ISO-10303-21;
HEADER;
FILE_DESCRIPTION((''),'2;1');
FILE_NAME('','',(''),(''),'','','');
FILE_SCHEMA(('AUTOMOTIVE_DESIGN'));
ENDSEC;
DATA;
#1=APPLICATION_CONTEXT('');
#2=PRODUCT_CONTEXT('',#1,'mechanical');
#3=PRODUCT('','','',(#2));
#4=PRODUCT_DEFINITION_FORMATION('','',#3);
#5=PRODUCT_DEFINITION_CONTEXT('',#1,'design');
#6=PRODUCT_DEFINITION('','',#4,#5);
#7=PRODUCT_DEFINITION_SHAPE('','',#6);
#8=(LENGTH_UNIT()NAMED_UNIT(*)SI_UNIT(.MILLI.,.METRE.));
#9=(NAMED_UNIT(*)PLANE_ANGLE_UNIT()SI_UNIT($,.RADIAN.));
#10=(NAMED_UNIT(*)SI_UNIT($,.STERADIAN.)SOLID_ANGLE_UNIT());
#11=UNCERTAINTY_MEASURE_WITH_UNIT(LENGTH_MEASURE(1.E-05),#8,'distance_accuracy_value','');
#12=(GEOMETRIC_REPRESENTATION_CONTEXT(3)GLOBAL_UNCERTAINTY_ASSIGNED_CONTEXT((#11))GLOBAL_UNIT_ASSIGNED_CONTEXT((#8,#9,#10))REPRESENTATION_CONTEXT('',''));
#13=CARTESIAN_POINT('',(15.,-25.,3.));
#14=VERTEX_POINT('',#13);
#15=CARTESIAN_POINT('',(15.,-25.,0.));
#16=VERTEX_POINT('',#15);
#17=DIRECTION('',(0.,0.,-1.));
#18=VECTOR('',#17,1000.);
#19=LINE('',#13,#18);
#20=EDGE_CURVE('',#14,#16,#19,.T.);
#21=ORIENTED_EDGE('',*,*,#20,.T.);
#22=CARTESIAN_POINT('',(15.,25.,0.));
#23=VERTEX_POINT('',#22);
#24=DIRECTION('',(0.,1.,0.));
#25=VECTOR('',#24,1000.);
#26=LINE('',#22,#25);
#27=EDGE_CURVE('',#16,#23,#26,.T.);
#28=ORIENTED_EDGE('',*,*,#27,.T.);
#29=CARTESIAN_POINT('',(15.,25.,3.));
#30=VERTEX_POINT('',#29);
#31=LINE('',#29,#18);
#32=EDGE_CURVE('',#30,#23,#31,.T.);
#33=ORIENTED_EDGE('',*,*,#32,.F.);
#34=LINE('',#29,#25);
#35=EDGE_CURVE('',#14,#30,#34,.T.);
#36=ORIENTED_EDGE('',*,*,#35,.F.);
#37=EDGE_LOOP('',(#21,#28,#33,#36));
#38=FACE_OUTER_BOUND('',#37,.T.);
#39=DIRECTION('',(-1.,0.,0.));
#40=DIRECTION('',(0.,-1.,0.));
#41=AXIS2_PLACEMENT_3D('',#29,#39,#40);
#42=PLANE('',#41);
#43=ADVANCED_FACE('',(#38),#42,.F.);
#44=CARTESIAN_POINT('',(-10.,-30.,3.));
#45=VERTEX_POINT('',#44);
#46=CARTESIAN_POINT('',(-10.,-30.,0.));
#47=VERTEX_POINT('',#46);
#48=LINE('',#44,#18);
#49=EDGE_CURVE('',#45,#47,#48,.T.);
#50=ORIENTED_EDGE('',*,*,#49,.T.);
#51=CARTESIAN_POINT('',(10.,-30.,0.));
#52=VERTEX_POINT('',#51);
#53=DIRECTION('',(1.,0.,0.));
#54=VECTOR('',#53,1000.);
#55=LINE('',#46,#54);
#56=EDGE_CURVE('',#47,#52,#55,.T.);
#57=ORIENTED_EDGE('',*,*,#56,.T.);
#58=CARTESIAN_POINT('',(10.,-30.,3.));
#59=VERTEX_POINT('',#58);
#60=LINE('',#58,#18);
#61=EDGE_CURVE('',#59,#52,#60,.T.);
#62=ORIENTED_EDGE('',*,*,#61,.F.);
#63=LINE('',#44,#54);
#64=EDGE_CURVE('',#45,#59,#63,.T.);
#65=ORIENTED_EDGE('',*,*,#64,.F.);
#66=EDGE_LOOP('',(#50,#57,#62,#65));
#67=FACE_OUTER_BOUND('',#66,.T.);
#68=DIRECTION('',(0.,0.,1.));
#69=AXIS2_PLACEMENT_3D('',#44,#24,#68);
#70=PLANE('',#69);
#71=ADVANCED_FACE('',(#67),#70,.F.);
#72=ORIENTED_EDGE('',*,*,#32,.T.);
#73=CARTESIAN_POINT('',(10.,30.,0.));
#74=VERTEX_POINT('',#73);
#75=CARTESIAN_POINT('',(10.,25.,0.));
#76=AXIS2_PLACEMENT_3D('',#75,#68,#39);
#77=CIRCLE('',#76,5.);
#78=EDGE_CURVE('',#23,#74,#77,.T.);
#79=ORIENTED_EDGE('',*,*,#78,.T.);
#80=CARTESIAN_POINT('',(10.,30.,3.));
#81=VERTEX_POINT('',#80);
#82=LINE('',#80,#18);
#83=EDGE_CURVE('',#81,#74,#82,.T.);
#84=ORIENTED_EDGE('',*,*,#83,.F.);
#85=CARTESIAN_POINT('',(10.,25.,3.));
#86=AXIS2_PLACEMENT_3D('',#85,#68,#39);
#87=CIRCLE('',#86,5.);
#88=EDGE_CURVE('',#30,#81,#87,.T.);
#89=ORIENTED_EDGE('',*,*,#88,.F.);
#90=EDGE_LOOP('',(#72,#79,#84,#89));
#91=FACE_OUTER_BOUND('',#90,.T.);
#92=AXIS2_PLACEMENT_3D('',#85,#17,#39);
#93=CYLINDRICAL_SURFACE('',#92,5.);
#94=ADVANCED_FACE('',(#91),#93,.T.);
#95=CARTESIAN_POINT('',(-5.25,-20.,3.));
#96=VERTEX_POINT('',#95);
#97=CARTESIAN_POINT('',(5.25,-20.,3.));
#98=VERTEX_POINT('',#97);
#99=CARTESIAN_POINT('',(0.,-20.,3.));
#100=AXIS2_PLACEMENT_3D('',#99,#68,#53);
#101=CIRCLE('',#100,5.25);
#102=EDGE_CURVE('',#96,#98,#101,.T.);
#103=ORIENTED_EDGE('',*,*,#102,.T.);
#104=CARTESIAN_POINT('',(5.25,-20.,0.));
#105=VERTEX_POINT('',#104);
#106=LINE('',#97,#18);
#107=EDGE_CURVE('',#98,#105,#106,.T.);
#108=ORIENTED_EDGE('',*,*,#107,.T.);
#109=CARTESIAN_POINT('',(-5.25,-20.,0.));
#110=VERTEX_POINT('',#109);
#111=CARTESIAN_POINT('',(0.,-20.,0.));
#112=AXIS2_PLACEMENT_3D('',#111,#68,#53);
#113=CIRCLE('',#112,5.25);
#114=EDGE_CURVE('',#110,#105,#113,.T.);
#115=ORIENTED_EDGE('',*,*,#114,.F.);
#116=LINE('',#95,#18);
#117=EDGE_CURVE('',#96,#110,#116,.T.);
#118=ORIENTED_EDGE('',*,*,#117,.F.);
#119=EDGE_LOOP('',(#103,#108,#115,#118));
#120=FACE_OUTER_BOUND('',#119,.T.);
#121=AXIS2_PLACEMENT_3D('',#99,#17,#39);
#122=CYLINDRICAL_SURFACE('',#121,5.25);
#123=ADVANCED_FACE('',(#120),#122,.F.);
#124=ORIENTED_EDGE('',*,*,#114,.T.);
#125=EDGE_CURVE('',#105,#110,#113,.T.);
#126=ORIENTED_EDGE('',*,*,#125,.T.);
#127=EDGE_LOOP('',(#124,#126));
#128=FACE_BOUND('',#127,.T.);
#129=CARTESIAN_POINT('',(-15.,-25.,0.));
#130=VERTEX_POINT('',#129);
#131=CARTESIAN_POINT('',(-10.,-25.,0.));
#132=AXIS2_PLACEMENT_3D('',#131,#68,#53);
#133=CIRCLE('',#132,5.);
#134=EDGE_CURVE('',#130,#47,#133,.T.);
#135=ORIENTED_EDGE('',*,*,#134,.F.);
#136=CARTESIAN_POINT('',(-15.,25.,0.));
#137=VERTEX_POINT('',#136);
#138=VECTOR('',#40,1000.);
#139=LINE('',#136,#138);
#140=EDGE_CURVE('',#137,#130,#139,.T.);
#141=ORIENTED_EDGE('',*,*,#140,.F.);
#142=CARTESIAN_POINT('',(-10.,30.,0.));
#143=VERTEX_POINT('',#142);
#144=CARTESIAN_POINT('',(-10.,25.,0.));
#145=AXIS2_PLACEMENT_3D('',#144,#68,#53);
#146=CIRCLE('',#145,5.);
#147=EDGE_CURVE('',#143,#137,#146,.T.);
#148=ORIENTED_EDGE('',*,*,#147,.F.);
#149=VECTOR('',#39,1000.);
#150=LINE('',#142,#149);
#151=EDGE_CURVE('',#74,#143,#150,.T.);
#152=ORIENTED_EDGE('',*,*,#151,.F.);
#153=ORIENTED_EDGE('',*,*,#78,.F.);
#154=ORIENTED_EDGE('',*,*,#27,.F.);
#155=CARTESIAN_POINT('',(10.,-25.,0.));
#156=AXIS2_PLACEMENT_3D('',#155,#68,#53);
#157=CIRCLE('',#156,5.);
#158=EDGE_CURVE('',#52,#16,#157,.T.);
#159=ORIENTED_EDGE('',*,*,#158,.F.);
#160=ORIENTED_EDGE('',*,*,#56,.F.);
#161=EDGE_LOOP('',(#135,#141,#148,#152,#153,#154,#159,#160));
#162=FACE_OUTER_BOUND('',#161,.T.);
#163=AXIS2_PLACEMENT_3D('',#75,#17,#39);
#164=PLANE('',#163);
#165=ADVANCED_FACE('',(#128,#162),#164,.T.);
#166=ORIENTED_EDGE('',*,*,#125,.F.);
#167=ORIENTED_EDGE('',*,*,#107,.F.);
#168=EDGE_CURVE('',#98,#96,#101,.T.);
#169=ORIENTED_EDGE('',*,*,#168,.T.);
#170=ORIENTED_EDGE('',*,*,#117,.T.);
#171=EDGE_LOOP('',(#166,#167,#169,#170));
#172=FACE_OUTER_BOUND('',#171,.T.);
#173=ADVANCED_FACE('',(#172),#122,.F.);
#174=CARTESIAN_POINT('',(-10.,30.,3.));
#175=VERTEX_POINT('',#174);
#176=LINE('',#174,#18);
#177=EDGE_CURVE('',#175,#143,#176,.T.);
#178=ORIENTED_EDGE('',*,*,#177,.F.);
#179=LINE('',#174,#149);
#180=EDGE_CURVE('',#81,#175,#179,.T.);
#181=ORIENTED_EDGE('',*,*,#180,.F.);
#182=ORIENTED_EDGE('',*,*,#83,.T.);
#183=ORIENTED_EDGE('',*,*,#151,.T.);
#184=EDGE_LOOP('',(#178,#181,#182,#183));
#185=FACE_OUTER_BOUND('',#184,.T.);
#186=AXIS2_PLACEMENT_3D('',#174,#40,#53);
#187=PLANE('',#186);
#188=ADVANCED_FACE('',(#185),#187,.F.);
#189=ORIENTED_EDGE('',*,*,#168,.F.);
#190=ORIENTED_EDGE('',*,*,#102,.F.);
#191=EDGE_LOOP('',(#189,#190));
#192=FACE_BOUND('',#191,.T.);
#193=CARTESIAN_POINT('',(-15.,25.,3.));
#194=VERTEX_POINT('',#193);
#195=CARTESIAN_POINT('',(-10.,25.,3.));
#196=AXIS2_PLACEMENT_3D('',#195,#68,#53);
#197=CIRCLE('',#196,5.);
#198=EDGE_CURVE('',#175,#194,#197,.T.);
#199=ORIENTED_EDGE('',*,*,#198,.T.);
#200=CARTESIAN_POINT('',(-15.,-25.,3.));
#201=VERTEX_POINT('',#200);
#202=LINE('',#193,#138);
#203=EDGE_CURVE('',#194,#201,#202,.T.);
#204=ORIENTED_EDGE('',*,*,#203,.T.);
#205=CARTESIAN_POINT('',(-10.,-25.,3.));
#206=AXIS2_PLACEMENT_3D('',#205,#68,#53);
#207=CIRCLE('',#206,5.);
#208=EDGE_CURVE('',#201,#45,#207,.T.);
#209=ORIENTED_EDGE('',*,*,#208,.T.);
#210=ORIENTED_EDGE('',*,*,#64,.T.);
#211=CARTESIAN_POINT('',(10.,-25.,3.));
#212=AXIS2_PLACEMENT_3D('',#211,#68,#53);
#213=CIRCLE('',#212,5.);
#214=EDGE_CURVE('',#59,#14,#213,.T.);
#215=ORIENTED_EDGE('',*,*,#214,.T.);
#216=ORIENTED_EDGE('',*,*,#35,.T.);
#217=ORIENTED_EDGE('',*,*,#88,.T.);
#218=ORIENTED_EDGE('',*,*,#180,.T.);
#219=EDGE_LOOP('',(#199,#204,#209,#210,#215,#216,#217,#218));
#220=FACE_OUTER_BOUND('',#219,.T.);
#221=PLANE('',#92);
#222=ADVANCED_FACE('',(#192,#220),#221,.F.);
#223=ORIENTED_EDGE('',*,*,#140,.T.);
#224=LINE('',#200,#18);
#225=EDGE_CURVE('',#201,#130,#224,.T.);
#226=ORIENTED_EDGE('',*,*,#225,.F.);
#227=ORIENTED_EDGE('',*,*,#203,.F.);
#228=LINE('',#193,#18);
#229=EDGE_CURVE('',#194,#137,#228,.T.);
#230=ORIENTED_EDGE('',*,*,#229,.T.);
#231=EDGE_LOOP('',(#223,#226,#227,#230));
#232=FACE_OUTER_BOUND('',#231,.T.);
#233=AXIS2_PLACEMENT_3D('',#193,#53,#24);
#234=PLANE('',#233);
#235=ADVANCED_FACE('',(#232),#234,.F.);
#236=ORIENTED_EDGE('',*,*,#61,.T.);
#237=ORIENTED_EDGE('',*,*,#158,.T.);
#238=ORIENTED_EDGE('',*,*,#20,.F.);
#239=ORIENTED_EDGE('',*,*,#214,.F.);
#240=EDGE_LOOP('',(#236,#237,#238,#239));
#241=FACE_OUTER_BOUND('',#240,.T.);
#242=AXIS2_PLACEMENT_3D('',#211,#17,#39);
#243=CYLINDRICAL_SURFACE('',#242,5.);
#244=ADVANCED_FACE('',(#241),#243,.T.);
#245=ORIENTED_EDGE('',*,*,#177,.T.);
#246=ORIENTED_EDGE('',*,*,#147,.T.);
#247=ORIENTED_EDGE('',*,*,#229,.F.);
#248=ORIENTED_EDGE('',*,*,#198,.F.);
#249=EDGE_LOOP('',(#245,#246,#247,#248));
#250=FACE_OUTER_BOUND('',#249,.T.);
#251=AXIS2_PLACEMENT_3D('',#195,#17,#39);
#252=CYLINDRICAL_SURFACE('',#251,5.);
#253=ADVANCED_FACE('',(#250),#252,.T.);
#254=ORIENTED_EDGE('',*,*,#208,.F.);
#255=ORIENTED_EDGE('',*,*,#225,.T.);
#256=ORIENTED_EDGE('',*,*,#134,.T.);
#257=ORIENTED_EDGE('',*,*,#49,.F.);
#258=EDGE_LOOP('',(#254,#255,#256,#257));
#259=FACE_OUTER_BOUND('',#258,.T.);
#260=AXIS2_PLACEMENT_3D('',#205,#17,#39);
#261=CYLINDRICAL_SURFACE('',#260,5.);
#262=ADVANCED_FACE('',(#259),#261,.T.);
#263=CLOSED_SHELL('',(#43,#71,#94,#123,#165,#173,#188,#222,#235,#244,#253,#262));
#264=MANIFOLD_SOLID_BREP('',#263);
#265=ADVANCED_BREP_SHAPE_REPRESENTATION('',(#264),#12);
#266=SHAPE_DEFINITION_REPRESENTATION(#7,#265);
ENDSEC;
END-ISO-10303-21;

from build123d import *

# Parameters (mm, degrees)
SKETCH1_R           = 5.25
BOSS_EXTRUDE1_DEPTH = 3


with BuildPart() as part:
    # Sketch1 → Boss-Extrude1 (new body)
    with BuildSketch(Plane.XY):
        with BuildLine():
            Line((-10, 30), (10, 30))
            ThreePointArc((10, 30), (13.535533906, 28.535533906), (15, 25))
            Line((15, 25), (15, -25))
            ThreePointArc((15, -25), (13.535533906, -28.535533906), (10, -30))
            Line((10, -30), (-10, -30))
            ThreePointArc((-10, -30), (-13.535533906, -28.535533906), (-15, -25))
            Line((-15, -25), (-15, 25))
            ThreePointArc((-15, 25), (-13.535533906, 28.535533906), (-10, 30))
        make_face()
        with Locations((0, -20)):
            Circle(SKETCH1_R, mode=Mode.SUBTRACT)
    extrude(amount=BOSS_EXTRUDE1_DEPTH)


solid = part.part
